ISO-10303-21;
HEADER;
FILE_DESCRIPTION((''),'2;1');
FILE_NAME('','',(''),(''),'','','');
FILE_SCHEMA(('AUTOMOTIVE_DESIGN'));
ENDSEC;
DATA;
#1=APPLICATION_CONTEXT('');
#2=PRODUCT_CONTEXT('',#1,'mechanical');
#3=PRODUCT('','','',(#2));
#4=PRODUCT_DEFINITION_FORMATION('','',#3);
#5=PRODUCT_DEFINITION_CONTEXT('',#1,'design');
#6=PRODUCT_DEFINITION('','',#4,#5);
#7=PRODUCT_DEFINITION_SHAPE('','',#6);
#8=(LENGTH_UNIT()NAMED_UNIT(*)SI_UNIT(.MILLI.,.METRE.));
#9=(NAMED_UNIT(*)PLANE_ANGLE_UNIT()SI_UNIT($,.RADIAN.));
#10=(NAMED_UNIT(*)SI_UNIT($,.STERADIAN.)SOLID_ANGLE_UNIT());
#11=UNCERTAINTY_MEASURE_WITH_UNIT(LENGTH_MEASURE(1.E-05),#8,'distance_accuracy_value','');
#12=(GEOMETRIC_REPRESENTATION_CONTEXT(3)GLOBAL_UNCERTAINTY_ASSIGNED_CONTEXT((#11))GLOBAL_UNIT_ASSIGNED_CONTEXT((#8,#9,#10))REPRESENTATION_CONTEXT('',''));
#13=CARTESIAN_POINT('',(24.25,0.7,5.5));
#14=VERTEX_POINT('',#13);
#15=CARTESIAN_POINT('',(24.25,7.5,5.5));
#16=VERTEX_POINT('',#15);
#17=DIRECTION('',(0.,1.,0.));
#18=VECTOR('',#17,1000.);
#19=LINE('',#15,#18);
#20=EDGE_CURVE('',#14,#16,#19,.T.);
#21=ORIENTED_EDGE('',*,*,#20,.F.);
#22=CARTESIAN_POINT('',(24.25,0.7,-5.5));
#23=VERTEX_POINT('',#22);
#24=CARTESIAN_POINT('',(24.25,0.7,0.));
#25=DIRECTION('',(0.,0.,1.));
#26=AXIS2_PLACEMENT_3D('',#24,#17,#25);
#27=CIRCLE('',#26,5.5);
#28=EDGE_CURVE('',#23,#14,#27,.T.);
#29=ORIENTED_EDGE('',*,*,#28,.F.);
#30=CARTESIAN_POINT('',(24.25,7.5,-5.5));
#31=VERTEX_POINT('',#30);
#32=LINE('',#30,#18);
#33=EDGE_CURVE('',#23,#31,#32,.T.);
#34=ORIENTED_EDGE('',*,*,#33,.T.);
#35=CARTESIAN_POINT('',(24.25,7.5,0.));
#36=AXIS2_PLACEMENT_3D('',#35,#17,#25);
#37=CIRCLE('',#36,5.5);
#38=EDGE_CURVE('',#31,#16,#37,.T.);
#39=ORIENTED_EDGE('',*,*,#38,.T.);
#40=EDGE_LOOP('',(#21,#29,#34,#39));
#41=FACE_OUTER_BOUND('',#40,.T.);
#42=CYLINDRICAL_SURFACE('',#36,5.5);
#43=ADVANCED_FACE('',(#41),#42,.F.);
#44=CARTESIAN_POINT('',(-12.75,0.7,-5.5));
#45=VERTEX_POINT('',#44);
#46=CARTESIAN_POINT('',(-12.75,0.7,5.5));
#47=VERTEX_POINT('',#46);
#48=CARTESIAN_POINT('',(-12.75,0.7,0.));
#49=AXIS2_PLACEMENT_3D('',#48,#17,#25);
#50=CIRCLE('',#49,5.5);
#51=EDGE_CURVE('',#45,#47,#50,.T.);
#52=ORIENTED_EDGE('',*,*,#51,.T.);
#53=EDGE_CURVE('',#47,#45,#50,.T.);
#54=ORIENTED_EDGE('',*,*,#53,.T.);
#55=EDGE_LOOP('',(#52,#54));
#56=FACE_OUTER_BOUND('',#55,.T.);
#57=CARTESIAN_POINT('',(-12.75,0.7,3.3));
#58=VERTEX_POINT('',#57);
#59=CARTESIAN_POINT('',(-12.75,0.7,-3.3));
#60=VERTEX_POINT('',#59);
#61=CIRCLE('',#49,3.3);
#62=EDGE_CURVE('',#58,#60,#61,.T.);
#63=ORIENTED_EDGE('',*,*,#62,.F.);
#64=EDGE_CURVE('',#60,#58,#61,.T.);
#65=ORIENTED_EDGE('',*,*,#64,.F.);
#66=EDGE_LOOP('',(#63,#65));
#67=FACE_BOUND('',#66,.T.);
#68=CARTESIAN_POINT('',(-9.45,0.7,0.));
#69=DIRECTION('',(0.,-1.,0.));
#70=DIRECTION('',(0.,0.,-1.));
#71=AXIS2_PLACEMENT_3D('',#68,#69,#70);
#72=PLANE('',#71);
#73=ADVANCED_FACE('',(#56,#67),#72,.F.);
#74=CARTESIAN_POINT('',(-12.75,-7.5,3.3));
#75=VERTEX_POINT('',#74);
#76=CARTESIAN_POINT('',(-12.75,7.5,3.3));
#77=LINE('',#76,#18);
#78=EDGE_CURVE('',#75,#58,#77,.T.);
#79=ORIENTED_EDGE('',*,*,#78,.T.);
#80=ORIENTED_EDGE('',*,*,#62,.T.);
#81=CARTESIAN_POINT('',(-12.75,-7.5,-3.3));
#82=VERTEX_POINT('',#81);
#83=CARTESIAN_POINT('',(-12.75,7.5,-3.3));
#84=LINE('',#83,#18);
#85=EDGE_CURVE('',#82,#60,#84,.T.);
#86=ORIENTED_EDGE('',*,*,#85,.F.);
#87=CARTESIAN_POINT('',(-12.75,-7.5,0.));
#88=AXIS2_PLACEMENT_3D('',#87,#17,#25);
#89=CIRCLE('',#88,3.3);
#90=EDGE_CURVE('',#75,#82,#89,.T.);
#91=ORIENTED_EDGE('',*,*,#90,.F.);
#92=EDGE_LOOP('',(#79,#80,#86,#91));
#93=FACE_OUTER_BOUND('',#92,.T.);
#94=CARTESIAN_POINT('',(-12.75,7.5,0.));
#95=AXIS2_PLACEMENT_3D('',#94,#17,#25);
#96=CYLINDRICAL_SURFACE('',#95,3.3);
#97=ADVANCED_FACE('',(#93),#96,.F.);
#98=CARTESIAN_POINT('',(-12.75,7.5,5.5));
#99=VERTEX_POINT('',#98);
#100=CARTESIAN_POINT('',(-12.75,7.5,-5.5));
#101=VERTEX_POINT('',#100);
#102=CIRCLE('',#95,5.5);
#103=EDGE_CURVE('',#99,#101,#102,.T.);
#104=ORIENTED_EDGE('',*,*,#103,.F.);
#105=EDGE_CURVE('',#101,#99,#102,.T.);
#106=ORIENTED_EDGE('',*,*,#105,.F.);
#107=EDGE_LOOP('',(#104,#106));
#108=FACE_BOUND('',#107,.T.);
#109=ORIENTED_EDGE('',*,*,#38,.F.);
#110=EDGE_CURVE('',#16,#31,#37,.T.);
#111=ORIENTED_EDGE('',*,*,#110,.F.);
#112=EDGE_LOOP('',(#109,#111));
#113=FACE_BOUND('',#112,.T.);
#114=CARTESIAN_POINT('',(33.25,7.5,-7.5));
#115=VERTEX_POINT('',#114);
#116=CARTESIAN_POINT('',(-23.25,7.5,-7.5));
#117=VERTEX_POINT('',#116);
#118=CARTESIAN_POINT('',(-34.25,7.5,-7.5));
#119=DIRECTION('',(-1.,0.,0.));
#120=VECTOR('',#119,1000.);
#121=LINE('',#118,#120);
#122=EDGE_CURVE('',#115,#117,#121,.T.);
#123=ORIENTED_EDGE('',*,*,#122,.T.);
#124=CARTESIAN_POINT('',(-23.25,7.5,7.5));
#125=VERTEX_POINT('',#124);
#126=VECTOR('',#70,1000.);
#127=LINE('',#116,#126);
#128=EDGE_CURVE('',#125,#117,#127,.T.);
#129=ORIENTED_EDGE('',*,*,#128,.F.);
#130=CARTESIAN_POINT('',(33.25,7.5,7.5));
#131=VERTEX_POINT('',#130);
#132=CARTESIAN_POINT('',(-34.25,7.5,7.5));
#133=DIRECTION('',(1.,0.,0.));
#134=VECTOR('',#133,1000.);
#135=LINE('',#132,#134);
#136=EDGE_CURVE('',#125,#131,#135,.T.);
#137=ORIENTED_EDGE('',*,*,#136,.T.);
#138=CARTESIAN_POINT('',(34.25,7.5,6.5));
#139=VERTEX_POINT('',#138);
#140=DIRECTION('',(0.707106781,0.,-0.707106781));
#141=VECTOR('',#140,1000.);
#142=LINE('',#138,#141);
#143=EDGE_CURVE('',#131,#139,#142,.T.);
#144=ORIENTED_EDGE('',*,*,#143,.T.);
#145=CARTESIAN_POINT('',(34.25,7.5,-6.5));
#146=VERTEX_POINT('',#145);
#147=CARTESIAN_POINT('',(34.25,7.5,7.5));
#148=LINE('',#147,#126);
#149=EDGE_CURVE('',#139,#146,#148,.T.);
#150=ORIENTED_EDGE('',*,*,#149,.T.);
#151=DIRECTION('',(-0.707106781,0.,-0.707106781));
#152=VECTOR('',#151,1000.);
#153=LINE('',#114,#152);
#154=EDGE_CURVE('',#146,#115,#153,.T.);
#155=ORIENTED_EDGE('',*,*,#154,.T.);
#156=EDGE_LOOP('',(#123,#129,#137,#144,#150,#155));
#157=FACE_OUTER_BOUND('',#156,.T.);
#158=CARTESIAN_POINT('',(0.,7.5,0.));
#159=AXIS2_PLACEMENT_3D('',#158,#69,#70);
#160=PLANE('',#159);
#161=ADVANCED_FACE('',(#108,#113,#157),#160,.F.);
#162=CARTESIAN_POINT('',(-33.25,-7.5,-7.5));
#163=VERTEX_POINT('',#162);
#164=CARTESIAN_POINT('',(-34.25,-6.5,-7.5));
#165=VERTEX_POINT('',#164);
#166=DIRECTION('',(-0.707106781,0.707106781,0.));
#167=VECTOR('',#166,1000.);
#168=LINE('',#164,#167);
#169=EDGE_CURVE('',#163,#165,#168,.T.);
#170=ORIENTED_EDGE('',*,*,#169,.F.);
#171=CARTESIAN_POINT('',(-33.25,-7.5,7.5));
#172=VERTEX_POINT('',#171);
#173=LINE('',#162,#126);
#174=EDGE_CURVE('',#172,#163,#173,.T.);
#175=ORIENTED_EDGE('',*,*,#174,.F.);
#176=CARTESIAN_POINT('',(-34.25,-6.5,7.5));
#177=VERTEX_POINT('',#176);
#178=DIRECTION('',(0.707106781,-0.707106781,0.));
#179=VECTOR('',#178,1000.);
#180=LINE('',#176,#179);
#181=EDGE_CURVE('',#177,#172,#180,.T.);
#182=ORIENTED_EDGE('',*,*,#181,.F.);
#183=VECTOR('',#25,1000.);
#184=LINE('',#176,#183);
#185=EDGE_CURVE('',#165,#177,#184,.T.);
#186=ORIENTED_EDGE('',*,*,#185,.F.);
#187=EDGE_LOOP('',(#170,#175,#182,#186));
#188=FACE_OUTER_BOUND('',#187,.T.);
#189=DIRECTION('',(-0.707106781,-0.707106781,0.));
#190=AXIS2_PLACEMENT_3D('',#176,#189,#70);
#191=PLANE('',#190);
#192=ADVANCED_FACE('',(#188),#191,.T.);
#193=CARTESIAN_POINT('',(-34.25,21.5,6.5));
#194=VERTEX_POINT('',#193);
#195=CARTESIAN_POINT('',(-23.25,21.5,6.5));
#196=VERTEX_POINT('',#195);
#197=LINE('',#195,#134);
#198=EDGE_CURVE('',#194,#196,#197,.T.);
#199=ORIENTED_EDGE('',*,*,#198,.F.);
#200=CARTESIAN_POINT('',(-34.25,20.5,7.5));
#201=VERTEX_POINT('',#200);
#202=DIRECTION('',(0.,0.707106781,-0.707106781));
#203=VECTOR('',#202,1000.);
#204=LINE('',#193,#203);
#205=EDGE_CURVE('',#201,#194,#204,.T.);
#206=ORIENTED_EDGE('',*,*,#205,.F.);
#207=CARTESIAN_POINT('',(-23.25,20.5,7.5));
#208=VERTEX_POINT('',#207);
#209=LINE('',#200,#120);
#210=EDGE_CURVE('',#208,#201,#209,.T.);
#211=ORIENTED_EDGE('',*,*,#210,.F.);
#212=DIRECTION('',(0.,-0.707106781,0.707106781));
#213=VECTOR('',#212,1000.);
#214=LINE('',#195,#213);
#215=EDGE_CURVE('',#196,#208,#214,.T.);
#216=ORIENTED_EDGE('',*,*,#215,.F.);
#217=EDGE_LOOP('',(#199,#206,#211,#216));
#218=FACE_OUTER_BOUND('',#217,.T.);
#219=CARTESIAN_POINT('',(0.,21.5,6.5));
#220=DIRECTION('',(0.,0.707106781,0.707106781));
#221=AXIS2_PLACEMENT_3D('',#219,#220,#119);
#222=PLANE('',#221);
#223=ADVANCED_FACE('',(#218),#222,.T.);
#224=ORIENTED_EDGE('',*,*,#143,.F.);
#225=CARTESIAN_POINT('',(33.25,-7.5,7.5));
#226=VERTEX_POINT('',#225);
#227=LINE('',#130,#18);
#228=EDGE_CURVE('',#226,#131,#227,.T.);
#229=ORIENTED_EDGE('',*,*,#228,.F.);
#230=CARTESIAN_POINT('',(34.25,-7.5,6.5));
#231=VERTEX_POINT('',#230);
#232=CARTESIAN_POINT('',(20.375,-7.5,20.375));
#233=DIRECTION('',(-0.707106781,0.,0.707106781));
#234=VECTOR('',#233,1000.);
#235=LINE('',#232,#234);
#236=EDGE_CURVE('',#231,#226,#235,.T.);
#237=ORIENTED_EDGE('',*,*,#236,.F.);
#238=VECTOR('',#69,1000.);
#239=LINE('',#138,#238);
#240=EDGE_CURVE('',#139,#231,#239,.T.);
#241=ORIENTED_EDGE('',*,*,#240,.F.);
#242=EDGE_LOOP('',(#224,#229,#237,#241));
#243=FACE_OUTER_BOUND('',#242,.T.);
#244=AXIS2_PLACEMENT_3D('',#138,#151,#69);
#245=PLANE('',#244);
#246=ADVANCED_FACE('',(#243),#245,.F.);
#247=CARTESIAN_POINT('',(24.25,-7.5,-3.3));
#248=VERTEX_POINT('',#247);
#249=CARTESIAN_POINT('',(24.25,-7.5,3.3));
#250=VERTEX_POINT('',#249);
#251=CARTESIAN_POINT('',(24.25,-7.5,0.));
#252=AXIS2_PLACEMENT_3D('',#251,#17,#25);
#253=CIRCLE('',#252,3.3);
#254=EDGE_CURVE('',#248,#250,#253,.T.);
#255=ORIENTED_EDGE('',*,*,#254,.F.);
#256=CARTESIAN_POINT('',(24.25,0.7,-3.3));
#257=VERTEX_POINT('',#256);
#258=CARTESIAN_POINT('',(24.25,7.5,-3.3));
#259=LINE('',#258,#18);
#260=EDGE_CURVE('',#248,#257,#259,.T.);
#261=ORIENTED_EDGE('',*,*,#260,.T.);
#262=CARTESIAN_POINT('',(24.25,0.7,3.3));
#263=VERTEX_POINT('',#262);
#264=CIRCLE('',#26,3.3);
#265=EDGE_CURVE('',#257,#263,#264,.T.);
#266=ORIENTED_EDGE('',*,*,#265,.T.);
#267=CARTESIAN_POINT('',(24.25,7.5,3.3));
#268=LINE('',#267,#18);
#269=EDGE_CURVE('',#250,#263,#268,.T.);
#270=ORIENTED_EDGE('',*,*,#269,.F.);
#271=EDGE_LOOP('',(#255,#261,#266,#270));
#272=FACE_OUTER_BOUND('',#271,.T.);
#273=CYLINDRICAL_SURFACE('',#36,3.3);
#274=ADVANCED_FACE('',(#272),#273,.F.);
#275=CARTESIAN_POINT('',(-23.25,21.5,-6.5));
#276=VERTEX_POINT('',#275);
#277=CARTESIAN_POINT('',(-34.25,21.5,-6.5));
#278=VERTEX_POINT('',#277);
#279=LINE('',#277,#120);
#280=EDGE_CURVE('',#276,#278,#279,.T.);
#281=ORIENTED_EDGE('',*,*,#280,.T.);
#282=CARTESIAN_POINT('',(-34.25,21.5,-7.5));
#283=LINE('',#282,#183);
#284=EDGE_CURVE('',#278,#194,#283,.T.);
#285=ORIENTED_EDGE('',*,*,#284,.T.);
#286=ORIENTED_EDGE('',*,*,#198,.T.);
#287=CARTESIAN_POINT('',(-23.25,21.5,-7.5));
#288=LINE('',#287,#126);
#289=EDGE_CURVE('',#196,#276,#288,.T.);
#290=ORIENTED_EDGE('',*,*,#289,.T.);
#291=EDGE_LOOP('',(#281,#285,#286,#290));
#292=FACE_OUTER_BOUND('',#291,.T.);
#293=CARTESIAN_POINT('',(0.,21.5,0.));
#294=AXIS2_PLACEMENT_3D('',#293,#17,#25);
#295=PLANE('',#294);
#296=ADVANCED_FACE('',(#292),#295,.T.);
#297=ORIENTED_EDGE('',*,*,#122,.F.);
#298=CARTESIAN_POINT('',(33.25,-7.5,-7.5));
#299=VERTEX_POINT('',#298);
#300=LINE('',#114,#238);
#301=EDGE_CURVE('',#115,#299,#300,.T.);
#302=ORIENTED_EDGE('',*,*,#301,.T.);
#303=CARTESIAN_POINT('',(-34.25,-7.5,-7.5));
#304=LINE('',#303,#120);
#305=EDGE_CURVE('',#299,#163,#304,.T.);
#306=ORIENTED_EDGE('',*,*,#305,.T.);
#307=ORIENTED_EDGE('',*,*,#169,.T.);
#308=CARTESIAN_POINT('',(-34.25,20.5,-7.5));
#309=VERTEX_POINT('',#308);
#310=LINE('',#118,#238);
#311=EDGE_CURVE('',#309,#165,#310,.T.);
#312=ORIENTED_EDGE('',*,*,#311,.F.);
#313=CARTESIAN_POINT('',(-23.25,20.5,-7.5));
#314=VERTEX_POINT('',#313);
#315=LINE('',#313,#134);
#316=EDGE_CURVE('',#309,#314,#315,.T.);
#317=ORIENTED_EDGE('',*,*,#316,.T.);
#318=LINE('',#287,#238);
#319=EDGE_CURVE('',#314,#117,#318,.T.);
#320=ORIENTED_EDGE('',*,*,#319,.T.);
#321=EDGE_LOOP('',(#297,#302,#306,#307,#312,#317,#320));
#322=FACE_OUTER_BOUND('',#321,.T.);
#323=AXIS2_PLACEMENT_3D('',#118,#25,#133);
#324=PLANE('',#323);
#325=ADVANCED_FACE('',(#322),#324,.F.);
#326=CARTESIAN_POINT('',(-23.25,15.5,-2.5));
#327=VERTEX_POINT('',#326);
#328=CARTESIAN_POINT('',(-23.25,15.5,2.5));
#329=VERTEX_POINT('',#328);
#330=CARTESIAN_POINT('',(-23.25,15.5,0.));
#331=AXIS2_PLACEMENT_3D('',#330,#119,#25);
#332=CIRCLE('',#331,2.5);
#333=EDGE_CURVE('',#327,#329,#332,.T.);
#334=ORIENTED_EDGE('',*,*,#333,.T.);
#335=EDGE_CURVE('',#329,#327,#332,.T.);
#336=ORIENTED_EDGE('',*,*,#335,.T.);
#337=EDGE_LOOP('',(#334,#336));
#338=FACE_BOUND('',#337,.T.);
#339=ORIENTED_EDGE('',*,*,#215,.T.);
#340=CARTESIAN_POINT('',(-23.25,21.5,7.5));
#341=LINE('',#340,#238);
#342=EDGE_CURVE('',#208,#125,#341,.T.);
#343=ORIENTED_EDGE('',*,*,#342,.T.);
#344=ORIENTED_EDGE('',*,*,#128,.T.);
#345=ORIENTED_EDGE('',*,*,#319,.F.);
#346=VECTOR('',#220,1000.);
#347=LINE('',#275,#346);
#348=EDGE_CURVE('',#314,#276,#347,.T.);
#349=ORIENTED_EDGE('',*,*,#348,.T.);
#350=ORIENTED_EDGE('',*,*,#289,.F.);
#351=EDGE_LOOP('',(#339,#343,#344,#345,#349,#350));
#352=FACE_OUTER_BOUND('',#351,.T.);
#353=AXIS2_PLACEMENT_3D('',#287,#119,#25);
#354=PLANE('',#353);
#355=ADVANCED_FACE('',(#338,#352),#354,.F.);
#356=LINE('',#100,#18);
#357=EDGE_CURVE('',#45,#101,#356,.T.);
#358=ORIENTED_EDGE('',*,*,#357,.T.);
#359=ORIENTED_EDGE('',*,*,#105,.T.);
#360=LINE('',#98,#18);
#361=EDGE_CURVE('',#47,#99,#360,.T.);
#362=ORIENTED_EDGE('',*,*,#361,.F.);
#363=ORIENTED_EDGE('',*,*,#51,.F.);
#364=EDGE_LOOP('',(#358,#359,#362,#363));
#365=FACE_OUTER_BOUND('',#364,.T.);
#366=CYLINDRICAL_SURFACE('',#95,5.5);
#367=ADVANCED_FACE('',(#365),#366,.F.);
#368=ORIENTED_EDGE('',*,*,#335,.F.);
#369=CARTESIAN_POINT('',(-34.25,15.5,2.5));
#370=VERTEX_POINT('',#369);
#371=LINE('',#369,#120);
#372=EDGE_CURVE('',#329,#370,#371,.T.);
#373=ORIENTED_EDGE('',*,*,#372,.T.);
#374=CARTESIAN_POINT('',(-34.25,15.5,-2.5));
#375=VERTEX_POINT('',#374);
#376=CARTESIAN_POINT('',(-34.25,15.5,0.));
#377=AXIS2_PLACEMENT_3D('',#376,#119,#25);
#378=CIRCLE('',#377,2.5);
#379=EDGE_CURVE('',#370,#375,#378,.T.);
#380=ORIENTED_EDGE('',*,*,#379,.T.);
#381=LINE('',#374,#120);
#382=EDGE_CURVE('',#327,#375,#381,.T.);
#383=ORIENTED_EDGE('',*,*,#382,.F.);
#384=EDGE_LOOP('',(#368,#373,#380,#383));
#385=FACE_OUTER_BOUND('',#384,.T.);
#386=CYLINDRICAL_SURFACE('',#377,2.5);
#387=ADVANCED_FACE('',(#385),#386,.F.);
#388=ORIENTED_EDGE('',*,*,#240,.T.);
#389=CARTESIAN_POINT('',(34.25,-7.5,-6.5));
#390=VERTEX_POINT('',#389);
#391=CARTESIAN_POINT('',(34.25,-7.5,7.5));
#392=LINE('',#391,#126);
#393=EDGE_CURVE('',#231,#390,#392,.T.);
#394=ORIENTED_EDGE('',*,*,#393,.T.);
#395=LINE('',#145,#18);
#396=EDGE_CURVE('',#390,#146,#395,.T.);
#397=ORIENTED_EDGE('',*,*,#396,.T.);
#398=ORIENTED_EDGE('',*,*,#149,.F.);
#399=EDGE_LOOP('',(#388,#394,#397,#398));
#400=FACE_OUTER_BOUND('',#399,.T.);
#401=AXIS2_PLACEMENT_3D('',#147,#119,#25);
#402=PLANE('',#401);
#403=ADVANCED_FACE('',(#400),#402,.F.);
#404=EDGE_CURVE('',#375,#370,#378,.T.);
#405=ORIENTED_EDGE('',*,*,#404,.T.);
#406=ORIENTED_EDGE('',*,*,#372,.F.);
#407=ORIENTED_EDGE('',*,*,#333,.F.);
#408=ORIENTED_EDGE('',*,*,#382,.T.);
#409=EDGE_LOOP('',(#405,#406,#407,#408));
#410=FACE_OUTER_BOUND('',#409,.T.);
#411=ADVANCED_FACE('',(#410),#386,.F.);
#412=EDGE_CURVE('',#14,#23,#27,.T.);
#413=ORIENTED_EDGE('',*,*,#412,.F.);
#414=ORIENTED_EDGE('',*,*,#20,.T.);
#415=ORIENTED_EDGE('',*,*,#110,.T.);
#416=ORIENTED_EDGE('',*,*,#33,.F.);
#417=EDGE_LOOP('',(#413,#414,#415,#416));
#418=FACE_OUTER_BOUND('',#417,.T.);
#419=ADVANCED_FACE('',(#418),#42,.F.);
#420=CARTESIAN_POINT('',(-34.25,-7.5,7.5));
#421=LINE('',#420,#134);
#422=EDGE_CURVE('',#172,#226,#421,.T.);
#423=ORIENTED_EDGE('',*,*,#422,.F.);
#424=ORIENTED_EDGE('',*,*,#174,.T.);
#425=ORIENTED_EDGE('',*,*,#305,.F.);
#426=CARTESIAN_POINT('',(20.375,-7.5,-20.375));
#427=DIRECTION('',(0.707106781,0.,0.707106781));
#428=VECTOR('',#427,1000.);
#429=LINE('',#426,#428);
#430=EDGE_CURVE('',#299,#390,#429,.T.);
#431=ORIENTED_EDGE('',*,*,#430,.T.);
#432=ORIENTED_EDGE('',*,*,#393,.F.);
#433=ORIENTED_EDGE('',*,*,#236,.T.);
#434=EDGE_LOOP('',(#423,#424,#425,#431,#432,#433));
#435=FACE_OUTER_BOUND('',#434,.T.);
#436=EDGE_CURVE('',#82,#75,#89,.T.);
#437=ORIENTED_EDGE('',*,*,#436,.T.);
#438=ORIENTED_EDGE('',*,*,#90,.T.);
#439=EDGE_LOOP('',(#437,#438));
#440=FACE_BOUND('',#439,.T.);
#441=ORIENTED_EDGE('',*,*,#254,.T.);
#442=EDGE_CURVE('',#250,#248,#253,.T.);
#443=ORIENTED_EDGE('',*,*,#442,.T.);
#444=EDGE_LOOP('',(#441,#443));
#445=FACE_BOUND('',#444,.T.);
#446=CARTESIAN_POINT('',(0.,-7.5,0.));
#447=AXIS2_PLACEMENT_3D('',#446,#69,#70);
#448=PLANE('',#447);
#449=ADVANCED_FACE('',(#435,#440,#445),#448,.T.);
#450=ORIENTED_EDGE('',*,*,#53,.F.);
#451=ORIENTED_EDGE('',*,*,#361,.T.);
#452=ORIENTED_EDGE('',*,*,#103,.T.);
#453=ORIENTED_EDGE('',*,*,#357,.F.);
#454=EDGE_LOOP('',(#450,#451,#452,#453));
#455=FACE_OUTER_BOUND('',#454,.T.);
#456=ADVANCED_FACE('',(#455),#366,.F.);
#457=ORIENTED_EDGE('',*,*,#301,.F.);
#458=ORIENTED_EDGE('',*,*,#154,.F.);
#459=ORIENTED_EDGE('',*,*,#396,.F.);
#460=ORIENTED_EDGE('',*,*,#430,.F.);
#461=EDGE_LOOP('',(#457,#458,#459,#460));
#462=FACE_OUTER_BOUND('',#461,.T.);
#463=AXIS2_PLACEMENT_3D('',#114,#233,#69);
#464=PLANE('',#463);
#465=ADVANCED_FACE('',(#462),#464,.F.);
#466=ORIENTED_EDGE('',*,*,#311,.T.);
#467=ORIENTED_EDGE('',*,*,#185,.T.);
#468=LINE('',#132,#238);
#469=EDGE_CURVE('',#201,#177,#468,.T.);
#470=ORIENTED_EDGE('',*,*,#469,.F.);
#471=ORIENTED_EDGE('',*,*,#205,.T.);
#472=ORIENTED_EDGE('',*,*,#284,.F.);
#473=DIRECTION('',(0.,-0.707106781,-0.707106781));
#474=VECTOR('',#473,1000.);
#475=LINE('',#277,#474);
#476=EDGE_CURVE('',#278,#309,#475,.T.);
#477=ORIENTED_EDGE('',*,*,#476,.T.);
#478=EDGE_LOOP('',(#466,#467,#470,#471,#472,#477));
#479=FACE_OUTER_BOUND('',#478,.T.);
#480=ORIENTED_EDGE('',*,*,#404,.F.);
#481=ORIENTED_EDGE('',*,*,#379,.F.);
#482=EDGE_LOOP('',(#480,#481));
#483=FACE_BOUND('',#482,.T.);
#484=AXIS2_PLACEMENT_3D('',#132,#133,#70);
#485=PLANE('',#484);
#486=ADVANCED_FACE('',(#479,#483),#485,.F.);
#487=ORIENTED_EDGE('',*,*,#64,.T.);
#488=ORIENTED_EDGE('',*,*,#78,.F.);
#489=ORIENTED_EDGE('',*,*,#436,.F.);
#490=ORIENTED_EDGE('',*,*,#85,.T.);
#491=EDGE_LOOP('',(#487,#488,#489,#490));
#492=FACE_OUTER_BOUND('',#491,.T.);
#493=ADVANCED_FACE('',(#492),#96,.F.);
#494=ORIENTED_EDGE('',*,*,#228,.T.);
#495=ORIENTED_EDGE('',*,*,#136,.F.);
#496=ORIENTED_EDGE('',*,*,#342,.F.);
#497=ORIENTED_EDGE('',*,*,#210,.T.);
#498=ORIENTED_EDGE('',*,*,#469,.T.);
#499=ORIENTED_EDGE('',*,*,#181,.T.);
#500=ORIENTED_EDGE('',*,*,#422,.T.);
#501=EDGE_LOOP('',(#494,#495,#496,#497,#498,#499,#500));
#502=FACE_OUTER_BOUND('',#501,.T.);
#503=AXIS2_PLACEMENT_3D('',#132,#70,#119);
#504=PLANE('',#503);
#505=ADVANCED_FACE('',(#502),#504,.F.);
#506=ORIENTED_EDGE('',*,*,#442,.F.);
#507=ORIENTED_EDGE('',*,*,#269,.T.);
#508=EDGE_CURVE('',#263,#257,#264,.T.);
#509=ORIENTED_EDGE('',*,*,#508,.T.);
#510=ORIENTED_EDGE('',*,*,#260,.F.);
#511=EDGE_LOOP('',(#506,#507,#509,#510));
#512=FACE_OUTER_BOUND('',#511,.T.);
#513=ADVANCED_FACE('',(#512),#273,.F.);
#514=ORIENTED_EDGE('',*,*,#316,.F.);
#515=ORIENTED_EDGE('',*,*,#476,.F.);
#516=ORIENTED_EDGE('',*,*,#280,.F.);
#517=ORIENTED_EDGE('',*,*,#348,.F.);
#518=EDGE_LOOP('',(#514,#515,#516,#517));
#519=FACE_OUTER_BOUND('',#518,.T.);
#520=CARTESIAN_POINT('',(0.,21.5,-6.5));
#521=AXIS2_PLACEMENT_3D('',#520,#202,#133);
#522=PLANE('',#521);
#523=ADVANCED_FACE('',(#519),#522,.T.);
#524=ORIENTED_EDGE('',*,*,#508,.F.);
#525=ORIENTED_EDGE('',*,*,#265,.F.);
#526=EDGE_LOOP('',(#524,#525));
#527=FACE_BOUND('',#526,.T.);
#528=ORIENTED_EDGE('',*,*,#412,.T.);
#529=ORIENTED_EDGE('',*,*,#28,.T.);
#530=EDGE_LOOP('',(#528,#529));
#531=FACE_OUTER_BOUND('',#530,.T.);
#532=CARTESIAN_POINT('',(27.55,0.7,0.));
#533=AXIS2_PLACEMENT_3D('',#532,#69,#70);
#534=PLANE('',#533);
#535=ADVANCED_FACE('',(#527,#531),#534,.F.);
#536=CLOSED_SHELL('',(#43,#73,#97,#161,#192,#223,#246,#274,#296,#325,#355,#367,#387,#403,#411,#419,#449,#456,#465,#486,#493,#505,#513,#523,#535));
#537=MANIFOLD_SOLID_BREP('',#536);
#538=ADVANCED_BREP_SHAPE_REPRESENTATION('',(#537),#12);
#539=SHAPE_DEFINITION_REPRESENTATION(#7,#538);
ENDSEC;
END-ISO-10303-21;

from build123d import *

# Parameters (mm, degrees)
SKETCH_1_W                   = 68.5
SKETCH_1_H                   = 15
EXTRUDE_1_DEPTH              = 7.5
SKETCH_2_W                   = 11
SKETCH_2_H                   = 15
EXTRUDE_2_DEPTH              = 14
CHAMFER_1_SIZE               = 1
HOLE_WIZARD_M6_1_D           = 6.6
HOLE_WIZARD_M6_1_CBORE_D     = 11
HOLE_WIZARD_M6_1_CBORE_DEPTH = 6.8
HOLE_WIZARD_M6_1_2_D         = 5


with BuildPart() as part:
    # 草图1 → 凸台-拉伸1 (new, symmetric)
    with BuildSketch(Plane(origin=(0, 0, 0), x_dir=(1, 0, 0), z_dir=(0, 1, 0))):
        Rectangle(SKETCH_1_W, SKETCH_1_H)
    extrude(amount=EXTRUDE_1_DEPTH, both=True)

    # 草图2 → 凸台-拉伸2 (add)
    with BuildSketch(Plane(origin=(0, 7.5, 0), x_dir=(1, 0, 0), z_dir=(0, 1, 0))):
        with Locations((-28.75, 0)):
            Rectangle(SKETCH_2_W, SKETCH_2_H)
    extrude(amount=EXTRUDE_2_DEPTH)

    # 倒角1
    chamfer_1_edges = [part.edges().sort_by_distance(p)[0] for p in [
        (-28.75, 21.5, 7.5),
        (-28.75, 21.5, -7.5),
        (-34.25, -7.5, 0),
        (34.25, 0, 7.5),
        (34.25, 0, -7.5),
    ]]
    chamfer(chamfer_1_edges, length=CHAMFER_1_SIZE)

    # Hole Wizard M6 _1 (through all)
    with Locations(Plane(origin=(0, 7.5, 0), x_dir=(1, 0, 0), z_dir=(0, 1, 0))):
        with Locations((24.25, 0), (-12.75, 0)):
            CounterBoreHole(HOLE_WIZARD_M6_1_D / 2, HOLE_WIZARD_M6_1_CBORE_D / 2, HOLE_WIZARD_M6_1_CBORE_DEPTH)

    # Hole Wizard M6 _1 2 (through all)
    with Locations(Plane.ZY.offset(34.25)):
        with Locations((0, 15.5)):
            Hole(HOLE_WIZARD_M6_1_2_D / 2)


solid = part.part
